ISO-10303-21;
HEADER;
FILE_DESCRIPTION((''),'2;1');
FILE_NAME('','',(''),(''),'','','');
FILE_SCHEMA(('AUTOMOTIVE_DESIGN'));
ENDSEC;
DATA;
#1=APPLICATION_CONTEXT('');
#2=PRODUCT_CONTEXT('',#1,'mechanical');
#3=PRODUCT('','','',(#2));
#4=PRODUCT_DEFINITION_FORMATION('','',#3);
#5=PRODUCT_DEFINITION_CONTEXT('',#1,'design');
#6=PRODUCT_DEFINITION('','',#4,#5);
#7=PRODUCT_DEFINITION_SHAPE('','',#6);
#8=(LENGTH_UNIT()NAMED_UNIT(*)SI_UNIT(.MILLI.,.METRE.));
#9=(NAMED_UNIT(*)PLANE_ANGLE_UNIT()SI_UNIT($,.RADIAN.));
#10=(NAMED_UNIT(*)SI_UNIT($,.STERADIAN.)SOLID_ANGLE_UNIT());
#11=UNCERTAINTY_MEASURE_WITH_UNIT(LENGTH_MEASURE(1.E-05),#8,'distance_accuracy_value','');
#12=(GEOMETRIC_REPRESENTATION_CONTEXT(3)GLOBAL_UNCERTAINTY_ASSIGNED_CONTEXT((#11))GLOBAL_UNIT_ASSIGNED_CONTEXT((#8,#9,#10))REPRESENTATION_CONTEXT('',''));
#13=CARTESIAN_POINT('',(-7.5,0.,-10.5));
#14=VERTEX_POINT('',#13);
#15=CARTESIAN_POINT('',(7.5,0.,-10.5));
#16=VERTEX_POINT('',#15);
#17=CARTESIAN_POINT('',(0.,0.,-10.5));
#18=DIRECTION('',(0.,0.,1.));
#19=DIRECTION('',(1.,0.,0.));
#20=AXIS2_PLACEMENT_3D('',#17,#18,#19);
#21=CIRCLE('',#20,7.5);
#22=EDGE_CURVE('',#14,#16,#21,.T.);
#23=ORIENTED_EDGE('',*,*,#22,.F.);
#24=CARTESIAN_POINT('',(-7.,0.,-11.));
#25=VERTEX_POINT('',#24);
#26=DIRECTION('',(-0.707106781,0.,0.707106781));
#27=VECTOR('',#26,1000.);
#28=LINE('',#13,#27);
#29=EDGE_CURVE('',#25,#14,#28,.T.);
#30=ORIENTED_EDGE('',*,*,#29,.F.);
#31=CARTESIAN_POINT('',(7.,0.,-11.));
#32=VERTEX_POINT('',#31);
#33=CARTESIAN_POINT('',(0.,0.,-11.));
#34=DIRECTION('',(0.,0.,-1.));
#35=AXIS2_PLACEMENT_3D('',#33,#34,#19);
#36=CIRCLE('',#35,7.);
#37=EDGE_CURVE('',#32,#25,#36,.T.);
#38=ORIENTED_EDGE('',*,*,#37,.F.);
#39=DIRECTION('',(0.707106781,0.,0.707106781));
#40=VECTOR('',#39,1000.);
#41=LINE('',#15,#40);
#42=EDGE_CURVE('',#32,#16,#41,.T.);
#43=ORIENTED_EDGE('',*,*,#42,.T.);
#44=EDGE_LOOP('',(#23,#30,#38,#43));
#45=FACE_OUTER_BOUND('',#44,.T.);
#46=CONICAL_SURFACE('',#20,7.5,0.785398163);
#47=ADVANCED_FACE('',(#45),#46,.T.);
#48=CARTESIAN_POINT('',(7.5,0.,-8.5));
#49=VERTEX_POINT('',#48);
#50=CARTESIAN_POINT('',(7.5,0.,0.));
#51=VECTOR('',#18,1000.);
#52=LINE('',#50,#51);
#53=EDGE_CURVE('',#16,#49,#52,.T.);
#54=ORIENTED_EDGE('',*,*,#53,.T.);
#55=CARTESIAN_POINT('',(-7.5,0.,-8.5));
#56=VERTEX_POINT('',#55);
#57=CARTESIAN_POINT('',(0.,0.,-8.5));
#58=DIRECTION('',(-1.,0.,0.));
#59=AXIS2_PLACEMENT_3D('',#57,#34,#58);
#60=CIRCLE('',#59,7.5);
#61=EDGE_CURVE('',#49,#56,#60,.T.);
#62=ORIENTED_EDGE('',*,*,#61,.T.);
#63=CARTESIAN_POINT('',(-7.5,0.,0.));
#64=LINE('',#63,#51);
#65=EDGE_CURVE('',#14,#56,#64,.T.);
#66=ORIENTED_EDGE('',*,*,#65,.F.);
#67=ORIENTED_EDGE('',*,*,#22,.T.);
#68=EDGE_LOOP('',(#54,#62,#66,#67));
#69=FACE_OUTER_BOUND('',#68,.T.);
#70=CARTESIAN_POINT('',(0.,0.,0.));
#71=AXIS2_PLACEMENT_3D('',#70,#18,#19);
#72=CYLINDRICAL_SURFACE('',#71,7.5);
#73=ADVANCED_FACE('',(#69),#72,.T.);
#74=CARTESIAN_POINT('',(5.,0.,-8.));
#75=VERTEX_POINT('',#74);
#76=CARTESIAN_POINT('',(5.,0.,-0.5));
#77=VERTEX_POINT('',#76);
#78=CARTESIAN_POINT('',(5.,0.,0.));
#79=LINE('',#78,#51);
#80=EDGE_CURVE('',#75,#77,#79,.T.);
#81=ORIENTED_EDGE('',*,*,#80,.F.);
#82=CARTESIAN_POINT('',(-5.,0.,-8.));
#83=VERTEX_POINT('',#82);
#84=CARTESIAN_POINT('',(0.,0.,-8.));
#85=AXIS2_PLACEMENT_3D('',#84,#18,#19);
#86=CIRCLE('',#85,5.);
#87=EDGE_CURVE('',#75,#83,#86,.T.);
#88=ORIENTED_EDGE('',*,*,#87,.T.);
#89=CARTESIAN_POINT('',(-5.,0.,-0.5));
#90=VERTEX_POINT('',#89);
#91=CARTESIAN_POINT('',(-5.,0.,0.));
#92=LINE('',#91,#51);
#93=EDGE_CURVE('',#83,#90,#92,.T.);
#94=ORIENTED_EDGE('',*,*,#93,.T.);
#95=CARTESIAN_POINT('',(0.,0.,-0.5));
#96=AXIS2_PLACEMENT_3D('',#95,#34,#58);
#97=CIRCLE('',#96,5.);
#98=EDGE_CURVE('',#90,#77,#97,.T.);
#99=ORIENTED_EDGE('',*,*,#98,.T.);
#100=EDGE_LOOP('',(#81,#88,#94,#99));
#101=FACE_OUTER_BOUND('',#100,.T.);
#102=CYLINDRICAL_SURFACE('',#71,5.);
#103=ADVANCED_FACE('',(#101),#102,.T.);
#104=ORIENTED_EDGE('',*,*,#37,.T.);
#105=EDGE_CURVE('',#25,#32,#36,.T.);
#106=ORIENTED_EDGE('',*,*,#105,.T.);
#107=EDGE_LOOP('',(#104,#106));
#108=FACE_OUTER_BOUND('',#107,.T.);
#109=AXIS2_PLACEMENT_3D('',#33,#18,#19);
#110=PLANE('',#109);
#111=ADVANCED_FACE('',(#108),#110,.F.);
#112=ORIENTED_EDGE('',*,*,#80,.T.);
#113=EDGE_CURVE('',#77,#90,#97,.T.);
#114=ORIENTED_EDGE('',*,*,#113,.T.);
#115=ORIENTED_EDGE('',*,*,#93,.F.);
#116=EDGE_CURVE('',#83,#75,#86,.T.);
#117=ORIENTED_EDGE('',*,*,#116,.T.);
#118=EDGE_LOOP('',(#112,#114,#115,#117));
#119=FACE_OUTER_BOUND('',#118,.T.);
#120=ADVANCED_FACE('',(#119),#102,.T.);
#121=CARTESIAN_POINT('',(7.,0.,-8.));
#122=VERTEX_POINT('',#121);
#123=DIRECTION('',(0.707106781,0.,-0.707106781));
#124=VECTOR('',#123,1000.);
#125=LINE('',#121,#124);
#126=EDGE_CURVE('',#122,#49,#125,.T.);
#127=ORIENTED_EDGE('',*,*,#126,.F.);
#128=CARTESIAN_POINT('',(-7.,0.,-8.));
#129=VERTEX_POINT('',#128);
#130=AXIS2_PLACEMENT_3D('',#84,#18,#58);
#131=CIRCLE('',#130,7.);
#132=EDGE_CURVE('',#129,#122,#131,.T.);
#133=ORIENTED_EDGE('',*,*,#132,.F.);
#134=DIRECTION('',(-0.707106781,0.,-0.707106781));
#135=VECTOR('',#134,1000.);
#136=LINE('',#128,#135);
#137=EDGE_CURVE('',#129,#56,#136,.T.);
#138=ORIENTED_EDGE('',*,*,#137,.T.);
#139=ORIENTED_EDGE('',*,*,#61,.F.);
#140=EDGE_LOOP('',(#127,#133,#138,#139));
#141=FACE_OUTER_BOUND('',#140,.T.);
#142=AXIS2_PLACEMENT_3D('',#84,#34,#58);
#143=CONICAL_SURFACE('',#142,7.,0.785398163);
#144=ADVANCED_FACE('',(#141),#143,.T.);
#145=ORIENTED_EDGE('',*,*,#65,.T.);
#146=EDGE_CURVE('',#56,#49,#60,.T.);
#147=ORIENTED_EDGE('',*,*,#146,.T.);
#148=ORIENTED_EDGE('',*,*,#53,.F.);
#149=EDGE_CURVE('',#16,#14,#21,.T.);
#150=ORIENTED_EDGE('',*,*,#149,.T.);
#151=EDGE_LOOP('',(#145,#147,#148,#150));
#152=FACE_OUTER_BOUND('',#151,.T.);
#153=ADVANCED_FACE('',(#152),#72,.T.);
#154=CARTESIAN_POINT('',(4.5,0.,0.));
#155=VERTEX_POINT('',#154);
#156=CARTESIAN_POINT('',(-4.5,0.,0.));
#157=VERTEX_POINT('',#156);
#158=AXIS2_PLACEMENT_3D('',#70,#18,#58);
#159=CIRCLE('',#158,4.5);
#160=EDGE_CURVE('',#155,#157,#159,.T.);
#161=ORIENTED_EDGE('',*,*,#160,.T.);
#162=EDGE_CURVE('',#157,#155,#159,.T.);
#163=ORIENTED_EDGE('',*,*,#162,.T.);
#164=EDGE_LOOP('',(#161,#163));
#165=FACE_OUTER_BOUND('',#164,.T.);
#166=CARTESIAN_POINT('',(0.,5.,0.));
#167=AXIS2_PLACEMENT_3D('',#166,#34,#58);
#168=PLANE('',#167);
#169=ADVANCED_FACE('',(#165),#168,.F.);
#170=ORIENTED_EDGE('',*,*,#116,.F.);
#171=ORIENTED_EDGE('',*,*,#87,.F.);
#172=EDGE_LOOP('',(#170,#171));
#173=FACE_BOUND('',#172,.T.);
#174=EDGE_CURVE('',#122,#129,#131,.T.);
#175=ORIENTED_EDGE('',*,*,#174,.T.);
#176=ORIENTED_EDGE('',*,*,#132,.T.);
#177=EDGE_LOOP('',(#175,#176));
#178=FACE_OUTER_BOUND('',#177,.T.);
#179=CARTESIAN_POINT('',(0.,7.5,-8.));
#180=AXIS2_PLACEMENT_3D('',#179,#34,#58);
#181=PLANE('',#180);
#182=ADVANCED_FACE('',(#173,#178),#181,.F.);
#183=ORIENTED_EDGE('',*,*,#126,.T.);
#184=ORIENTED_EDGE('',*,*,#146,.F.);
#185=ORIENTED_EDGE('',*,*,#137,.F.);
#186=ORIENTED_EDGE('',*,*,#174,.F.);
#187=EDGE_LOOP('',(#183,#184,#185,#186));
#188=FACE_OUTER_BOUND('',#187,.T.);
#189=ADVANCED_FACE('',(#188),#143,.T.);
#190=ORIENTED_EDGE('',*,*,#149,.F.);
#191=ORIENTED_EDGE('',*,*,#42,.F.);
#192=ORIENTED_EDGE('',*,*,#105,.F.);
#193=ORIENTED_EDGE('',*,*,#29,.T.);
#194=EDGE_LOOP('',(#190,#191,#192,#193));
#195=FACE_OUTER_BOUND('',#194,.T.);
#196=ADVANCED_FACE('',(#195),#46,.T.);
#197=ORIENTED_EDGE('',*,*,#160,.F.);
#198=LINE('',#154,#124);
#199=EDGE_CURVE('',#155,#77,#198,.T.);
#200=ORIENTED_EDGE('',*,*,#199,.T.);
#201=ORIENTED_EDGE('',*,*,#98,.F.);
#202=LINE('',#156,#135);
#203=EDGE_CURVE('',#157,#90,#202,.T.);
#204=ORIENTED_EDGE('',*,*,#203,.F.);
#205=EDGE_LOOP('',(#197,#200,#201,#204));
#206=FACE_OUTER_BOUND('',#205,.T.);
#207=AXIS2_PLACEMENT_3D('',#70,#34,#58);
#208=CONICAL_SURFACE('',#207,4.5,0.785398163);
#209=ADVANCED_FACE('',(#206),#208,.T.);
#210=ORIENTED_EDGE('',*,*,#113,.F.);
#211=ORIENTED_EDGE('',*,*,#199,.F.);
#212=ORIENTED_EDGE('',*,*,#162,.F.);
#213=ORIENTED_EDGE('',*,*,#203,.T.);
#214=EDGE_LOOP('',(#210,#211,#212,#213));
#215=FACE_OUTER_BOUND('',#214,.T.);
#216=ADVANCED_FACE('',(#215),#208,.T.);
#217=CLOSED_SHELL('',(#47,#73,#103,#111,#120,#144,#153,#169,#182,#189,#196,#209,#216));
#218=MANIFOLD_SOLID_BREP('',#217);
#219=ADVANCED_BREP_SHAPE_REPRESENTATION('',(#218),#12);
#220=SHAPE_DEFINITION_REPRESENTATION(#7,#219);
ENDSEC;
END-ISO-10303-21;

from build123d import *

# Parameters (mm, degrees)
CHAMFER1_SIZE = 0.5


with BuildPart() as part:
    # Sketch1 → Revolve1 (revolve)
    with BuildSketch(Plane(origin=(0, 0, 0), x_dir=(0, 0, -1), z_dir=(1, 0, 0)), mode=Mode.PRIVATE) as revolve1_sk:
        Polygon((11, 0), (11, 7.5), (8, 7.5), (8, 5), (0, 5), (0, 0), align=None)
    revolve(revolve1_sk.sketch.rotate(Axis((0, 0, 0), (0, 0, -1)), 90), axis=Axis((0, 0, 0), (0, 0, -1)))

    # Chamfer1
    chamfer1_edges = [part.edges().sort_by_distance(p)[0] for p in [
        (-5, 0, 0),
        (-7.5, 0, -8),
        (-7.5, 0, -11),
    ]]
    chamfer(chamfer1_edges, length=CHAMFER1_SIZE)


solid = part.part
